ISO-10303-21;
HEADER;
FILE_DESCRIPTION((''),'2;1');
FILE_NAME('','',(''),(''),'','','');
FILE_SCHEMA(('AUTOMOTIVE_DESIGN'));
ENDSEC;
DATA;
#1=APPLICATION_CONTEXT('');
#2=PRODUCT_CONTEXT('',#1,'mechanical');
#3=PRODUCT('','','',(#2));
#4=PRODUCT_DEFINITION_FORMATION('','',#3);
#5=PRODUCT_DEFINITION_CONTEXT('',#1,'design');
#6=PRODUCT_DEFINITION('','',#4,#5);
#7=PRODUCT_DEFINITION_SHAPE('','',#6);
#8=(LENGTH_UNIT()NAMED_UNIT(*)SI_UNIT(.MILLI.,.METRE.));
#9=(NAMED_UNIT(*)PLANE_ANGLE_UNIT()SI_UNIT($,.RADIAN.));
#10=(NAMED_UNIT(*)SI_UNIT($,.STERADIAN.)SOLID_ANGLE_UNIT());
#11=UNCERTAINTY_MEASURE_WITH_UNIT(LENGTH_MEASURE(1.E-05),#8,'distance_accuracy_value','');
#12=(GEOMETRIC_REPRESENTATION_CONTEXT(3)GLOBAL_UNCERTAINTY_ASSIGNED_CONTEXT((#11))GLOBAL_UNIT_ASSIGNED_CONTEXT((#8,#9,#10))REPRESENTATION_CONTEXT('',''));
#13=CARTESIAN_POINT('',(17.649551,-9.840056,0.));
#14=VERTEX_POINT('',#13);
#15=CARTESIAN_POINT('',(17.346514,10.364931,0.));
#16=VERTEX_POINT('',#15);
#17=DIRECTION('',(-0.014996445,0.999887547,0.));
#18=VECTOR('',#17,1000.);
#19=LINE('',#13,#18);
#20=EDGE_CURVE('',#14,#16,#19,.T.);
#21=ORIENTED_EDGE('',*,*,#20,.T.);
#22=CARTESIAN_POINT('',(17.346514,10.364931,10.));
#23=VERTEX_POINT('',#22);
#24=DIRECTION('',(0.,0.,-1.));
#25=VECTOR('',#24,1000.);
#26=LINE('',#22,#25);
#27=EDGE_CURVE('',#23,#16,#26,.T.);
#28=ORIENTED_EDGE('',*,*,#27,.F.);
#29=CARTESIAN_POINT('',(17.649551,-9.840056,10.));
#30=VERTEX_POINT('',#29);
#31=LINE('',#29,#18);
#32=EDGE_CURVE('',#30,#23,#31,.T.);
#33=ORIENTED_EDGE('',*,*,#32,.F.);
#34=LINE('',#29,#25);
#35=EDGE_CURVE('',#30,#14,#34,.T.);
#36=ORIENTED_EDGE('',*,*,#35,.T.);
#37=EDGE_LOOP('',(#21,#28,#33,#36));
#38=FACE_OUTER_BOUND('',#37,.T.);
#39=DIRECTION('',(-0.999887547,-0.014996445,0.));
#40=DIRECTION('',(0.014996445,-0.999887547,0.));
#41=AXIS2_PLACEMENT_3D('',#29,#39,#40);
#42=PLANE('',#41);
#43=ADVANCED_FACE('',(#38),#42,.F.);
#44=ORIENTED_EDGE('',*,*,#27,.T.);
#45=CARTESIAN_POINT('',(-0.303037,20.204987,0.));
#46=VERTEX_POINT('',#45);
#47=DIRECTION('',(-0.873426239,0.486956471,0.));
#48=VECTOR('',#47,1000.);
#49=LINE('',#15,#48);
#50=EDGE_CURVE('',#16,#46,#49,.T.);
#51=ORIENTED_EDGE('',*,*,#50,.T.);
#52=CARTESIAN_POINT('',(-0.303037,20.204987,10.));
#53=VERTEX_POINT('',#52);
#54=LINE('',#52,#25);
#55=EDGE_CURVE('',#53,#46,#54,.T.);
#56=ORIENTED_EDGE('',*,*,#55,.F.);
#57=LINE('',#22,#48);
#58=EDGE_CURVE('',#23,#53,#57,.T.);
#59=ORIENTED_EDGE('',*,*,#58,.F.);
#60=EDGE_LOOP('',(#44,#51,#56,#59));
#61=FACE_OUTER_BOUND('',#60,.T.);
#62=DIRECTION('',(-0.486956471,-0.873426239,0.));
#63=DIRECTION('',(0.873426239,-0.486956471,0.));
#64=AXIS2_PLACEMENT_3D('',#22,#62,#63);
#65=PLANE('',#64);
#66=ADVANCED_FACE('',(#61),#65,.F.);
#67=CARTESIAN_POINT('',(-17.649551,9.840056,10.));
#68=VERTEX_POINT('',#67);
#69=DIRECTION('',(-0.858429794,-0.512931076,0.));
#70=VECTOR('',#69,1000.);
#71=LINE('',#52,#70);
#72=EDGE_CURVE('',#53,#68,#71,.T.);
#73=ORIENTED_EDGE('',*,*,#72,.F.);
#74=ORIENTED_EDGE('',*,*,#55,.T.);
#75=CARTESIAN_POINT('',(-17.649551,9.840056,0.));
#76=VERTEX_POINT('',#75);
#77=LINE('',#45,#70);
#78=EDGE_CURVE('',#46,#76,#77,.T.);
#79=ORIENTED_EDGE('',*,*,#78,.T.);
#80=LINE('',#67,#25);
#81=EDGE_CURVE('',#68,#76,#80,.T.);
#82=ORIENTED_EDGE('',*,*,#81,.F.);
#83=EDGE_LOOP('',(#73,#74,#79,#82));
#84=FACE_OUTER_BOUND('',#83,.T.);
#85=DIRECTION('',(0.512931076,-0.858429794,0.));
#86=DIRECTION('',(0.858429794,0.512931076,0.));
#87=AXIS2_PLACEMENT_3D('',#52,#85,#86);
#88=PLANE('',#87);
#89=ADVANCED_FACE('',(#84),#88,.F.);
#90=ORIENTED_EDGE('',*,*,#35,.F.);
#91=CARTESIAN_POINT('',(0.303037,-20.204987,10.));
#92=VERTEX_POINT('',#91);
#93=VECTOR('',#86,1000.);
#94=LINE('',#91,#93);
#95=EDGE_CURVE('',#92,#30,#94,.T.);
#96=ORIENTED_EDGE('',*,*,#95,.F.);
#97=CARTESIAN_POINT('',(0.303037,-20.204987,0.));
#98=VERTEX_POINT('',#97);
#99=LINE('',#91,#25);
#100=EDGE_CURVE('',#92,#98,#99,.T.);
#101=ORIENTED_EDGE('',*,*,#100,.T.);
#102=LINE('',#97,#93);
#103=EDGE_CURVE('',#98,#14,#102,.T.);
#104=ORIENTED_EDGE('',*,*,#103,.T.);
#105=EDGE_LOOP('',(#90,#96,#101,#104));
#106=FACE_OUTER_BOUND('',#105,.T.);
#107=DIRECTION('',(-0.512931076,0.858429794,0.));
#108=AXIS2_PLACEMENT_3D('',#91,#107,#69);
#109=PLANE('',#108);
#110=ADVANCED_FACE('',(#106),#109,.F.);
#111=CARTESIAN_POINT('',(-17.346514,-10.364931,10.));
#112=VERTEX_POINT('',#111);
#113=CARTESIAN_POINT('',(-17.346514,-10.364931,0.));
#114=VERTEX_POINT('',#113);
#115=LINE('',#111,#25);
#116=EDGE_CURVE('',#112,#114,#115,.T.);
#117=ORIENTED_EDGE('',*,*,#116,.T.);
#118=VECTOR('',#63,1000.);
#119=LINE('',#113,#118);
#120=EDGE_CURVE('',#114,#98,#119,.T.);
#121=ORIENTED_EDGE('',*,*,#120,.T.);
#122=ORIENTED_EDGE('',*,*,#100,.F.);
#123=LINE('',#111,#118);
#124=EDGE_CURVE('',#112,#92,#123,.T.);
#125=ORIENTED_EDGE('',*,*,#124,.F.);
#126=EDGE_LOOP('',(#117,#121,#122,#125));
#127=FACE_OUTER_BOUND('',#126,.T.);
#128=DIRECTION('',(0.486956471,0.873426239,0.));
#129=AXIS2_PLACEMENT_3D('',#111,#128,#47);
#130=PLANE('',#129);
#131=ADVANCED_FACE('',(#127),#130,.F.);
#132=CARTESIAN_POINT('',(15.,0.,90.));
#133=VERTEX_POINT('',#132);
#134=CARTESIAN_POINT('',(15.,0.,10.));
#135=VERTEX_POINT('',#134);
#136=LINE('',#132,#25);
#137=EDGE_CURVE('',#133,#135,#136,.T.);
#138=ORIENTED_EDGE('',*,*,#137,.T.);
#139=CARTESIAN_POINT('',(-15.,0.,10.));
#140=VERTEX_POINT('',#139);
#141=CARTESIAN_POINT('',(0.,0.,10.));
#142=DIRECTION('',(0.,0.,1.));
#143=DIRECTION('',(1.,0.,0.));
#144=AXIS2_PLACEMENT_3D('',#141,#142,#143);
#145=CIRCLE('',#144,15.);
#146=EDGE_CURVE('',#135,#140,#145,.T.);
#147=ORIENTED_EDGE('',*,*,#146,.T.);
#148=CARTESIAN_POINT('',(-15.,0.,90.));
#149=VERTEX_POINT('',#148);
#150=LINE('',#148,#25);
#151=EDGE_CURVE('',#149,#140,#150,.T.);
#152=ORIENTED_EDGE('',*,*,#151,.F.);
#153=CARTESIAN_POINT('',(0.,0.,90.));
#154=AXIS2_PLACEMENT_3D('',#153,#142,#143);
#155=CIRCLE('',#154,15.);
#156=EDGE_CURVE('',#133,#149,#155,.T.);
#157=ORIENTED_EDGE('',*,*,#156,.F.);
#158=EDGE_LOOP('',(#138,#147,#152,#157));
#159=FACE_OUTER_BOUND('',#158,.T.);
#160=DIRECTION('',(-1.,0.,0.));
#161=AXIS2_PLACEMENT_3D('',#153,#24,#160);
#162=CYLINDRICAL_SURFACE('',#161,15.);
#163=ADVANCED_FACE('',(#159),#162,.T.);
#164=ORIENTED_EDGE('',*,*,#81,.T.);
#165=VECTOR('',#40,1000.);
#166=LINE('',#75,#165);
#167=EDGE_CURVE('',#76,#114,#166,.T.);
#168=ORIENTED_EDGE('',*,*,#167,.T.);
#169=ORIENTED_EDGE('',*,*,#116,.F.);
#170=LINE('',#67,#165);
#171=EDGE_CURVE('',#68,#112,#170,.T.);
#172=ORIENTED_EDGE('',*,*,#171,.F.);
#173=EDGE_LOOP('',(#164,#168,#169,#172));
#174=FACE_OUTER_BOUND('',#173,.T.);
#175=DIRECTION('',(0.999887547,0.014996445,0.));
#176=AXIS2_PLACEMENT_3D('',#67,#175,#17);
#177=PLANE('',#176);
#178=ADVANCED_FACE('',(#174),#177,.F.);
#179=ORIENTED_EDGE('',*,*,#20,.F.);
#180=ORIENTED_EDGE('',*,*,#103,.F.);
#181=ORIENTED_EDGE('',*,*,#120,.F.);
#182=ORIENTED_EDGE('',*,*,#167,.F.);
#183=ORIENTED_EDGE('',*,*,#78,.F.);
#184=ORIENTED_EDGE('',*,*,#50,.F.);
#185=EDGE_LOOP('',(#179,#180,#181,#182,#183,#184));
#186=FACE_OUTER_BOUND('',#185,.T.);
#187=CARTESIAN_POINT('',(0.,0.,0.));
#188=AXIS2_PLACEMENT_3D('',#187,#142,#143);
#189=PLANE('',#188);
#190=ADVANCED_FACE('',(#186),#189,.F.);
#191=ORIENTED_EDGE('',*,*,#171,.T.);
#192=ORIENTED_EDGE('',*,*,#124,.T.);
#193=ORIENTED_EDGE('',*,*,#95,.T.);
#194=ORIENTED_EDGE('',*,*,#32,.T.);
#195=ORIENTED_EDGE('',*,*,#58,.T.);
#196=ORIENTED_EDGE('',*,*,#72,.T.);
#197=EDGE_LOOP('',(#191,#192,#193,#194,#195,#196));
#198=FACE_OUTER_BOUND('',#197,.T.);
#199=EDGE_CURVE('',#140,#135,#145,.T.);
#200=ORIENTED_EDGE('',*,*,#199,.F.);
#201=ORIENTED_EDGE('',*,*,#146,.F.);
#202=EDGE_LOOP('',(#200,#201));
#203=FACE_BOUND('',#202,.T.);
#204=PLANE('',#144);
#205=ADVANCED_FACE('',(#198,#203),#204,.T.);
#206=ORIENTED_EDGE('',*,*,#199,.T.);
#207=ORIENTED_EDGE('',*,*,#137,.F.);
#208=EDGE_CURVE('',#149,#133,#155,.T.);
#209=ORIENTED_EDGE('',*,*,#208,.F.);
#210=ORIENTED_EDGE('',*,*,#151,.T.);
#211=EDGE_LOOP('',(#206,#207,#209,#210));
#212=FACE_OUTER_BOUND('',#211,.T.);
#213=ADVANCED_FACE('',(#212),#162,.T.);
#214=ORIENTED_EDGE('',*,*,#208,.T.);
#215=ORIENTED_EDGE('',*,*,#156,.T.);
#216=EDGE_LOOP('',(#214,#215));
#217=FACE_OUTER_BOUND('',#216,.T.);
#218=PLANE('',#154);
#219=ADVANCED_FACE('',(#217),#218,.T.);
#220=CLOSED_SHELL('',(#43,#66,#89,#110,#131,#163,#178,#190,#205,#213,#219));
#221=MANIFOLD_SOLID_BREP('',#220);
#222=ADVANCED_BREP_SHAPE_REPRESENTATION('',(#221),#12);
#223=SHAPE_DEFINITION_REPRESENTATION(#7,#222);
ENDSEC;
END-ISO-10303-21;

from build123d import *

# Parameters (mm, degrees)
BOSS_EXTRUDE1_DEPTH = 10
SKETCH2_R           = 15
BOSS_EXTRUDE2_DEPTH = 80


with BuildPart() as part:
    # Sketch1 → Boss-Extrude1 (new body)
    with BuildSketch(Plane.XY):
        Polygon((17.346513547, 10.364931312), (-0.303037051, 20.204987055), (-17.649550598, 9.840055742), (-17.346513547, -10.364931312), (0.303037051, -20.204987055), (17.649550598, -9.840055742), align=None)
    extrude(amount=BOSS_EXTRUDE1_DEPTH)

    # Sketch2 → Boss-Extrude2 (add)
    with BuildSketch(Plane.XY.offset(10)):
        Circle(SKETCH2_R)
    extrude(amount=BOSS_EXTRUDE2_DEPTH)


solid = part.part
